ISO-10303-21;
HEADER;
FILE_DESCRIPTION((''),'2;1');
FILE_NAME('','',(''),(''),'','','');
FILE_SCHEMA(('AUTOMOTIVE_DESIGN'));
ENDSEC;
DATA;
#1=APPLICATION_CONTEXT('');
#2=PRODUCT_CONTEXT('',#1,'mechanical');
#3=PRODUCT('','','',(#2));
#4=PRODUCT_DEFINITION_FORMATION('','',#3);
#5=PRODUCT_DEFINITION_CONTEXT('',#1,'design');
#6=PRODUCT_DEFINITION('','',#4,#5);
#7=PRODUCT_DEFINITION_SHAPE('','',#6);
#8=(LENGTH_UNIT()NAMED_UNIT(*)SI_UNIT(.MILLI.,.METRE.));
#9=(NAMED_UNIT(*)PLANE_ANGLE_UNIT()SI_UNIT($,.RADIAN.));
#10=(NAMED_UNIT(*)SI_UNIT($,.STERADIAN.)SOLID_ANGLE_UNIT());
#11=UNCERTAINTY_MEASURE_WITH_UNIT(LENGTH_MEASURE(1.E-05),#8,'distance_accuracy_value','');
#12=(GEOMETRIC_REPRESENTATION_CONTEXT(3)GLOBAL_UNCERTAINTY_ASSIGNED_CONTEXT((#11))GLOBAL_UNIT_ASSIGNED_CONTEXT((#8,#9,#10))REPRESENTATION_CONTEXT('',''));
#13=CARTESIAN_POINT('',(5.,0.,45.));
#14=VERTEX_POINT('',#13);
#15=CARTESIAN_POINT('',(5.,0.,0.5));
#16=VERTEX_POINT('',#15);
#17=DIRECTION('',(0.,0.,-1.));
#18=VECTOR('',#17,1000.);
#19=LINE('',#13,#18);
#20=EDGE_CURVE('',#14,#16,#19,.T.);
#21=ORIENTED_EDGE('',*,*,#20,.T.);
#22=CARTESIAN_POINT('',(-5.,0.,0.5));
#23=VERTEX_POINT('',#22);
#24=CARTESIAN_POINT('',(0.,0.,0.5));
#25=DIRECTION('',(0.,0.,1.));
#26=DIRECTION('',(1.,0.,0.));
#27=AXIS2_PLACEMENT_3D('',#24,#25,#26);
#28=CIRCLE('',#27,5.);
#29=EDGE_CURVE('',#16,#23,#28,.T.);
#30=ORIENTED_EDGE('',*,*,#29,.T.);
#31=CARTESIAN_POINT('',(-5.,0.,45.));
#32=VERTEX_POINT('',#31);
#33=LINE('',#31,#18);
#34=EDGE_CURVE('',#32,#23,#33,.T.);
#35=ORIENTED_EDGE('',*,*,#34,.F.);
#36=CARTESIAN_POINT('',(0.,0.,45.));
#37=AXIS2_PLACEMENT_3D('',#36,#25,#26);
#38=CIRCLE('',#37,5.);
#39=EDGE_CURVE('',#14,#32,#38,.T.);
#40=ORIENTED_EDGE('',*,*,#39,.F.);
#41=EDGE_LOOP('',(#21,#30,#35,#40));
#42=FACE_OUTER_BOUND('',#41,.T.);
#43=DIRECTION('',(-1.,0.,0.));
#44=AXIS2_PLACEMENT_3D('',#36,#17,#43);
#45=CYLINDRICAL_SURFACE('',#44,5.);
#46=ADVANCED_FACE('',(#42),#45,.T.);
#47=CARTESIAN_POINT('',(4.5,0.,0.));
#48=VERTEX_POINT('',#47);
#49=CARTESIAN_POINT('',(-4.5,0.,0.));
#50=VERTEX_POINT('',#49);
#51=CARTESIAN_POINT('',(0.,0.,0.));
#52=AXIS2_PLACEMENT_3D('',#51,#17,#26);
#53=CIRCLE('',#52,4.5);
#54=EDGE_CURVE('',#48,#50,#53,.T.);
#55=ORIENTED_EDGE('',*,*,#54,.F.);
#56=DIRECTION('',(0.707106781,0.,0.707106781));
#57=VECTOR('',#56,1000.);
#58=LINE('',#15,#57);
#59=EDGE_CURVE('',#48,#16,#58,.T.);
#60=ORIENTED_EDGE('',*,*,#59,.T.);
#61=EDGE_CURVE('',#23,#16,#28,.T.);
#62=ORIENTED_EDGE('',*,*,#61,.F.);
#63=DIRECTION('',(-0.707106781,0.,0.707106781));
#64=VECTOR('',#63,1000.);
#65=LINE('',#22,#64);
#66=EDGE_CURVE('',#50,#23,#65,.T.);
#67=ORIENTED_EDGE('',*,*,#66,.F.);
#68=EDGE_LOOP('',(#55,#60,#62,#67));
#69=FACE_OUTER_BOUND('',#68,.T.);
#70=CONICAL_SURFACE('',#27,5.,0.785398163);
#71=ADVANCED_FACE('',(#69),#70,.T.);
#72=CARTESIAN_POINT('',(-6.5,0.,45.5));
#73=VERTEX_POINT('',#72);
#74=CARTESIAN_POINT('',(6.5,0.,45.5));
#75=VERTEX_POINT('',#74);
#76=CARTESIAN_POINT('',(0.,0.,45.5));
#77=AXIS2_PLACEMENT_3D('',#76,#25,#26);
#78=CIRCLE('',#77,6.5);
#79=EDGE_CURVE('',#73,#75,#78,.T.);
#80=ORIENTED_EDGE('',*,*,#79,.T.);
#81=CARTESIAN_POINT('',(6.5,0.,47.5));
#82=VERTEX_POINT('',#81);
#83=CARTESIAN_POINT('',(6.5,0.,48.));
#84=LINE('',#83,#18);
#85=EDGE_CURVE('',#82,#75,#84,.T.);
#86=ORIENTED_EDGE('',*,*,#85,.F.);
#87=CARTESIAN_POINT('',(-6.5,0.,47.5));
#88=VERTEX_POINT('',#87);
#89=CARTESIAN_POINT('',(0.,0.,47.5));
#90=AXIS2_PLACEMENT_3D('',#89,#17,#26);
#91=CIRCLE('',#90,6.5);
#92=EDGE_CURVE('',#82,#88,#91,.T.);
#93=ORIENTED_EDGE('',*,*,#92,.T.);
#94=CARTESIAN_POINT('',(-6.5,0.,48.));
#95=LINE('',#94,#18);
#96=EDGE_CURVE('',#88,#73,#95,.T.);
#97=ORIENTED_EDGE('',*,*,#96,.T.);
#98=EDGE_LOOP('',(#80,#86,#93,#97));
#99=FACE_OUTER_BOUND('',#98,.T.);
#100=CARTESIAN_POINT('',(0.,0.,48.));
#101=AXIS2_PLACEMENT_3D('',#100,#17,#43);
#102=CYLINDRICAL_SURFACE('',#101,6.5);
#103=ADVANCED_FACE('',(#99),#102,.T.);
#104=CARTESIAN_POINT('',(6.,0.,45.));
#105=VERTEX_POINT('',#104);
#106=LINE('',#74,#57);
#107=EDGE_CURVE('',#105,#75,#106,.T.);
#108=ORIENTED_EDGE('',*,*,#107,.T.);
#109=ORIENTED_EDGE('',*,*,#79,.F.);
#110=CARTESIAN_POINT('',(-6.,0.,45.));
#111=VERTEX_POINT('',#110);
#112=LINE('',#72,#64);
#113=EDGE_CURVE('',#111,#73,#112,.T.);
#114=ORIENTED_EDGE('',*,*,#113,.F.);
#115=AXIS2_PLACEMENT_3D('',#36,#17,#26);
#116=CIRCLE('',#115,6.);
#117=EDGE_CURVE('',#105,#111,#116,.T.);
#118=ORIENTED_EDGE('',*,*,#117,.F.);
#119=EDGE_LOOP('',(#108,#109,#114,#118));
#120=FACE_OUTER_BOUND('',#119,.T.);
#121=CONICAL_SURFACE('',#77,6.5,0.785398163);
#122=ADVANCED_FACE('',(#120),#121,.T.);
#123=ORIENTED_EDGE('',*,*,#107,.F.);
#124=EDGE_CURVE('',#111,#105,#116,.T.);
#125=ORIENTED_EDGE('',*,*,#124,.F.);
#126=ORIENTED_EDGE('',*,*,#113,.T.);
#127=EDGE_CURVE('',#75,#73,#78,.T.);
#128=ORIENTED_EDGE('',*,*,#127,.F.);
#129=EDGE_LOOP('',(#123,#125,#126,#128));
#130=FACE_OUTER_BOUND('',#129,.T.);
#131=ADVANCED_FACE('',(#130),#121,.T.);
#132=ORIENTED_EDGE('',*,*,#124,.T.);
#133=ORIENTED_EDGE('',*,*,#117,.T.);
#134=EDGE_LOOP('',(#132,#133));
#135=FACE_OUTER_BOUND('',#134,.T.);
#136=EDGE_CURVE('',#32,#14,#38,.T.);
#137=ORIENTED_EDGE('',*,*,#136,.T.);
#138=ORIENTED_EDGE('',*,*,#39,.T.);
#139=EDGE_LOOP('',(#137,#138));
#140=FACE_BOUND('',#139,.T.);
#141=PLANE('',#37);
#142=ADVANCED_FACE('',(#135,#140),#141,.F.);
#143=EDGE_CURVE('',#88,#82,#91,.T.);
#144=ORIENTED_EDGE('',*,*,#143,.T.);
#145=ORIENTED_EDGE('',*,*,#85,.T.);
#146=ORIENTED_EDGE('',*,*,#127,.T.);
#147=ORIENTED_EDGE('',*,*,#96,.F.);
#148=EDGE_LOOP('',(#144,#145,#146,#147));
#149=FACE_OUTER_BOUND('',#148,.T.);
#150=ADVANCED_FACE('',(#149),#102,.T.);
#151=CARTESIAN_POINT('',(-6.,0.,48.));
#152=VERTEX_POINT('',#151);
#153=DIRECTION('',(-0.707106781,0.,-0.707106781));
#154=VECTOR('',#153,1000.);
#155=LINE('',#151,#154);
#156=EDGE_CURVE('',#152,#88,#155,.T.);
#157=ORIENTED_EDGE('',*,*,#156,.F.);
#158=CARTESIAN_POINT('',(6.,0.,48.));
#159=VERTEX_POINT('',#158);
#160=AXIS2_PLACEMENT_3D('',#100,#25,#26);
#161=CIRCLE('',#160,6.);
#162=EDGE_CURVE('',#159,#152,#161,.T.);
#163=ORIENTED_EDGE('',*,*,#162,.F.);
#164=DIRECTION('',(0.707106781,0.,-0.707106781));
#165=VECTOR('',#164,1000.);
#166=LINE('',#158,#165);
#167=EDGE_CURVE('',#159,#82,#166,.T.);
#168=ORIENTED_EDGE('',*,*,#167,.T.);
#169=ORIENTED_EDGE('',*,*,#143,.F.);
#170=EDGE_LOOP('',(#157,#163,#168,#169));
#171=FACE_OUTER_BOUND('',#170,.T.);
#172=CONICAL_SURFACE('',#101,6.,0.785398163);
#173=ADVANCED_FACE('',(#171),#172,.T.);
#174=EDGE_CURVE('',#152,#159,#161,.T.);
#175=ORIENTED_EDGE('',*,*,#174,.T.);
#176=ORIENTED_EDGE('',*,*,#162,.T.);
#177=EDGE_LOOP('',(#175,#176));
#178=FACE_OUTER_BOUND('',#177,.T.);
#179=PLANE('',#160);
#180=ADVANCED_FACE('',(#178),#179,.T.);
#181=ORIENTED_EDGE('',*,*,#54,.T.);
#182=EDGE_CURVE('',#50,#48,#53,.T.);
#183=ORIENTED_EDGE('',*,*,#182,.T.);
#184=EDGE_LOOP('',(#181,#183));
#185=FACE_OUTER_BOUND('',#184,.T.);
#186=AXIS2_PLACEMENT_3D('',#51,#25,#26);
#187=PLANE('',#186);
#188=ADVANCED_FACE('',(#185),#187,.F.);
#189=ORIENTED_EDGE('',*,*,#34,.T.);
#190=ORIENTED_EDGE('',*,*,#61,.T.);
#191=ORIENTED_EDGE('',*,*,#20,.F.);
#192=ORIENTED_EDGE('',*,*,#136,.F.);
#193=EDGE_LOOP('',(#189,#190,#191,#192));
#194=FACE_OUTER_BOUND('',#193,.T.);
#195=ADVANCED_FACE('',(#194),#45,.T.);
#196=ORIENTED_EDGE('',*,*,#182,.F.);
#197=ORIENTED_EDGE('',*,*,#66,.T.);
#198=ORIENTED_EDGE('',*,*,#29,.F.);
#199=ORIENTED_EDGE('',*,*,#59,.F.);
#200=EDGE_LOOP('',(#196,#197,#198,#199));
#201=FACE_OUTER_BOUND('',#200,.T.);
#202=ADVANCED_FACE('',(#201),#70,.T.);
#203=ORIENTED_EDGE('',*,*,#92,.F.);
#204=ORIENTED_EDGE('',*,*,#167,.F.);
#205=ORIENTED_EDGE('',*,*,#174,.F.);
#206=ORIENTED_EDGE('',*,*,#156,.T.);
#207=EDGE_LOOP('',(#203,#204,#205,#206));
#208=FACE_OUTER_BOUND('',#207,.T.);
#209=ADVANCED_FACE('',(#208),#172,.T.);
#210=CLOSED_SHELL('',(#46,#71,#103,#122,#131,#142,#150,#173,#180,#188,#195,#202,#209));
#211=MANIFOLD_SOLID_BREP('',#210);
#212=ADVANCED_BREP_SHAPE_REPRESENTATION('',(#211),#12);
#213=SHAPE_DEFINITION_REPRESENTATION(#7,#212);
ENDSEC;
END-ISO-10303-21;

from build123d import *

# Parameters (mm, degrees)
SKETCH1_R           = 5
BOSS_EXTRUDE1_DEPTH = 45
SKETCH2_R           = 6.5
BOSS_EXTRUDE2_DEPTH = 3
CHAMFER1_SIZE       = 0.5


with BuildPart() as part:
    # Sketch1 → Boss-Extrude1 (new body)
    with BuildSketch(Plane.XY):
        with Locations(Location((0, 0, 0), (0, 0, 180))):
            Circle(SKETCH1_R)
    extrude(amount=BOSS_EXTRUDE1_DEPTH)

    # Sketch2 → Boss-Extrude2 (add)
    with BuildSketch(Plane.XY.offset(45)):
        Circle(SKETCH2_R)
    extrude(amount=BOSS_EXTRUDE2_DEPTH)

    # Chamfer1
    chamfer1_edges = [part.edges().sort_by_distance(p)[0] for p in [
        (5, 0, 0),
        (-6.5, 0, 45),
        (-6.5, 0, 48),
    ]]
    chamfer(chamfer1_edges, length=CHAMFER1_SIZE)


solid = part.part
